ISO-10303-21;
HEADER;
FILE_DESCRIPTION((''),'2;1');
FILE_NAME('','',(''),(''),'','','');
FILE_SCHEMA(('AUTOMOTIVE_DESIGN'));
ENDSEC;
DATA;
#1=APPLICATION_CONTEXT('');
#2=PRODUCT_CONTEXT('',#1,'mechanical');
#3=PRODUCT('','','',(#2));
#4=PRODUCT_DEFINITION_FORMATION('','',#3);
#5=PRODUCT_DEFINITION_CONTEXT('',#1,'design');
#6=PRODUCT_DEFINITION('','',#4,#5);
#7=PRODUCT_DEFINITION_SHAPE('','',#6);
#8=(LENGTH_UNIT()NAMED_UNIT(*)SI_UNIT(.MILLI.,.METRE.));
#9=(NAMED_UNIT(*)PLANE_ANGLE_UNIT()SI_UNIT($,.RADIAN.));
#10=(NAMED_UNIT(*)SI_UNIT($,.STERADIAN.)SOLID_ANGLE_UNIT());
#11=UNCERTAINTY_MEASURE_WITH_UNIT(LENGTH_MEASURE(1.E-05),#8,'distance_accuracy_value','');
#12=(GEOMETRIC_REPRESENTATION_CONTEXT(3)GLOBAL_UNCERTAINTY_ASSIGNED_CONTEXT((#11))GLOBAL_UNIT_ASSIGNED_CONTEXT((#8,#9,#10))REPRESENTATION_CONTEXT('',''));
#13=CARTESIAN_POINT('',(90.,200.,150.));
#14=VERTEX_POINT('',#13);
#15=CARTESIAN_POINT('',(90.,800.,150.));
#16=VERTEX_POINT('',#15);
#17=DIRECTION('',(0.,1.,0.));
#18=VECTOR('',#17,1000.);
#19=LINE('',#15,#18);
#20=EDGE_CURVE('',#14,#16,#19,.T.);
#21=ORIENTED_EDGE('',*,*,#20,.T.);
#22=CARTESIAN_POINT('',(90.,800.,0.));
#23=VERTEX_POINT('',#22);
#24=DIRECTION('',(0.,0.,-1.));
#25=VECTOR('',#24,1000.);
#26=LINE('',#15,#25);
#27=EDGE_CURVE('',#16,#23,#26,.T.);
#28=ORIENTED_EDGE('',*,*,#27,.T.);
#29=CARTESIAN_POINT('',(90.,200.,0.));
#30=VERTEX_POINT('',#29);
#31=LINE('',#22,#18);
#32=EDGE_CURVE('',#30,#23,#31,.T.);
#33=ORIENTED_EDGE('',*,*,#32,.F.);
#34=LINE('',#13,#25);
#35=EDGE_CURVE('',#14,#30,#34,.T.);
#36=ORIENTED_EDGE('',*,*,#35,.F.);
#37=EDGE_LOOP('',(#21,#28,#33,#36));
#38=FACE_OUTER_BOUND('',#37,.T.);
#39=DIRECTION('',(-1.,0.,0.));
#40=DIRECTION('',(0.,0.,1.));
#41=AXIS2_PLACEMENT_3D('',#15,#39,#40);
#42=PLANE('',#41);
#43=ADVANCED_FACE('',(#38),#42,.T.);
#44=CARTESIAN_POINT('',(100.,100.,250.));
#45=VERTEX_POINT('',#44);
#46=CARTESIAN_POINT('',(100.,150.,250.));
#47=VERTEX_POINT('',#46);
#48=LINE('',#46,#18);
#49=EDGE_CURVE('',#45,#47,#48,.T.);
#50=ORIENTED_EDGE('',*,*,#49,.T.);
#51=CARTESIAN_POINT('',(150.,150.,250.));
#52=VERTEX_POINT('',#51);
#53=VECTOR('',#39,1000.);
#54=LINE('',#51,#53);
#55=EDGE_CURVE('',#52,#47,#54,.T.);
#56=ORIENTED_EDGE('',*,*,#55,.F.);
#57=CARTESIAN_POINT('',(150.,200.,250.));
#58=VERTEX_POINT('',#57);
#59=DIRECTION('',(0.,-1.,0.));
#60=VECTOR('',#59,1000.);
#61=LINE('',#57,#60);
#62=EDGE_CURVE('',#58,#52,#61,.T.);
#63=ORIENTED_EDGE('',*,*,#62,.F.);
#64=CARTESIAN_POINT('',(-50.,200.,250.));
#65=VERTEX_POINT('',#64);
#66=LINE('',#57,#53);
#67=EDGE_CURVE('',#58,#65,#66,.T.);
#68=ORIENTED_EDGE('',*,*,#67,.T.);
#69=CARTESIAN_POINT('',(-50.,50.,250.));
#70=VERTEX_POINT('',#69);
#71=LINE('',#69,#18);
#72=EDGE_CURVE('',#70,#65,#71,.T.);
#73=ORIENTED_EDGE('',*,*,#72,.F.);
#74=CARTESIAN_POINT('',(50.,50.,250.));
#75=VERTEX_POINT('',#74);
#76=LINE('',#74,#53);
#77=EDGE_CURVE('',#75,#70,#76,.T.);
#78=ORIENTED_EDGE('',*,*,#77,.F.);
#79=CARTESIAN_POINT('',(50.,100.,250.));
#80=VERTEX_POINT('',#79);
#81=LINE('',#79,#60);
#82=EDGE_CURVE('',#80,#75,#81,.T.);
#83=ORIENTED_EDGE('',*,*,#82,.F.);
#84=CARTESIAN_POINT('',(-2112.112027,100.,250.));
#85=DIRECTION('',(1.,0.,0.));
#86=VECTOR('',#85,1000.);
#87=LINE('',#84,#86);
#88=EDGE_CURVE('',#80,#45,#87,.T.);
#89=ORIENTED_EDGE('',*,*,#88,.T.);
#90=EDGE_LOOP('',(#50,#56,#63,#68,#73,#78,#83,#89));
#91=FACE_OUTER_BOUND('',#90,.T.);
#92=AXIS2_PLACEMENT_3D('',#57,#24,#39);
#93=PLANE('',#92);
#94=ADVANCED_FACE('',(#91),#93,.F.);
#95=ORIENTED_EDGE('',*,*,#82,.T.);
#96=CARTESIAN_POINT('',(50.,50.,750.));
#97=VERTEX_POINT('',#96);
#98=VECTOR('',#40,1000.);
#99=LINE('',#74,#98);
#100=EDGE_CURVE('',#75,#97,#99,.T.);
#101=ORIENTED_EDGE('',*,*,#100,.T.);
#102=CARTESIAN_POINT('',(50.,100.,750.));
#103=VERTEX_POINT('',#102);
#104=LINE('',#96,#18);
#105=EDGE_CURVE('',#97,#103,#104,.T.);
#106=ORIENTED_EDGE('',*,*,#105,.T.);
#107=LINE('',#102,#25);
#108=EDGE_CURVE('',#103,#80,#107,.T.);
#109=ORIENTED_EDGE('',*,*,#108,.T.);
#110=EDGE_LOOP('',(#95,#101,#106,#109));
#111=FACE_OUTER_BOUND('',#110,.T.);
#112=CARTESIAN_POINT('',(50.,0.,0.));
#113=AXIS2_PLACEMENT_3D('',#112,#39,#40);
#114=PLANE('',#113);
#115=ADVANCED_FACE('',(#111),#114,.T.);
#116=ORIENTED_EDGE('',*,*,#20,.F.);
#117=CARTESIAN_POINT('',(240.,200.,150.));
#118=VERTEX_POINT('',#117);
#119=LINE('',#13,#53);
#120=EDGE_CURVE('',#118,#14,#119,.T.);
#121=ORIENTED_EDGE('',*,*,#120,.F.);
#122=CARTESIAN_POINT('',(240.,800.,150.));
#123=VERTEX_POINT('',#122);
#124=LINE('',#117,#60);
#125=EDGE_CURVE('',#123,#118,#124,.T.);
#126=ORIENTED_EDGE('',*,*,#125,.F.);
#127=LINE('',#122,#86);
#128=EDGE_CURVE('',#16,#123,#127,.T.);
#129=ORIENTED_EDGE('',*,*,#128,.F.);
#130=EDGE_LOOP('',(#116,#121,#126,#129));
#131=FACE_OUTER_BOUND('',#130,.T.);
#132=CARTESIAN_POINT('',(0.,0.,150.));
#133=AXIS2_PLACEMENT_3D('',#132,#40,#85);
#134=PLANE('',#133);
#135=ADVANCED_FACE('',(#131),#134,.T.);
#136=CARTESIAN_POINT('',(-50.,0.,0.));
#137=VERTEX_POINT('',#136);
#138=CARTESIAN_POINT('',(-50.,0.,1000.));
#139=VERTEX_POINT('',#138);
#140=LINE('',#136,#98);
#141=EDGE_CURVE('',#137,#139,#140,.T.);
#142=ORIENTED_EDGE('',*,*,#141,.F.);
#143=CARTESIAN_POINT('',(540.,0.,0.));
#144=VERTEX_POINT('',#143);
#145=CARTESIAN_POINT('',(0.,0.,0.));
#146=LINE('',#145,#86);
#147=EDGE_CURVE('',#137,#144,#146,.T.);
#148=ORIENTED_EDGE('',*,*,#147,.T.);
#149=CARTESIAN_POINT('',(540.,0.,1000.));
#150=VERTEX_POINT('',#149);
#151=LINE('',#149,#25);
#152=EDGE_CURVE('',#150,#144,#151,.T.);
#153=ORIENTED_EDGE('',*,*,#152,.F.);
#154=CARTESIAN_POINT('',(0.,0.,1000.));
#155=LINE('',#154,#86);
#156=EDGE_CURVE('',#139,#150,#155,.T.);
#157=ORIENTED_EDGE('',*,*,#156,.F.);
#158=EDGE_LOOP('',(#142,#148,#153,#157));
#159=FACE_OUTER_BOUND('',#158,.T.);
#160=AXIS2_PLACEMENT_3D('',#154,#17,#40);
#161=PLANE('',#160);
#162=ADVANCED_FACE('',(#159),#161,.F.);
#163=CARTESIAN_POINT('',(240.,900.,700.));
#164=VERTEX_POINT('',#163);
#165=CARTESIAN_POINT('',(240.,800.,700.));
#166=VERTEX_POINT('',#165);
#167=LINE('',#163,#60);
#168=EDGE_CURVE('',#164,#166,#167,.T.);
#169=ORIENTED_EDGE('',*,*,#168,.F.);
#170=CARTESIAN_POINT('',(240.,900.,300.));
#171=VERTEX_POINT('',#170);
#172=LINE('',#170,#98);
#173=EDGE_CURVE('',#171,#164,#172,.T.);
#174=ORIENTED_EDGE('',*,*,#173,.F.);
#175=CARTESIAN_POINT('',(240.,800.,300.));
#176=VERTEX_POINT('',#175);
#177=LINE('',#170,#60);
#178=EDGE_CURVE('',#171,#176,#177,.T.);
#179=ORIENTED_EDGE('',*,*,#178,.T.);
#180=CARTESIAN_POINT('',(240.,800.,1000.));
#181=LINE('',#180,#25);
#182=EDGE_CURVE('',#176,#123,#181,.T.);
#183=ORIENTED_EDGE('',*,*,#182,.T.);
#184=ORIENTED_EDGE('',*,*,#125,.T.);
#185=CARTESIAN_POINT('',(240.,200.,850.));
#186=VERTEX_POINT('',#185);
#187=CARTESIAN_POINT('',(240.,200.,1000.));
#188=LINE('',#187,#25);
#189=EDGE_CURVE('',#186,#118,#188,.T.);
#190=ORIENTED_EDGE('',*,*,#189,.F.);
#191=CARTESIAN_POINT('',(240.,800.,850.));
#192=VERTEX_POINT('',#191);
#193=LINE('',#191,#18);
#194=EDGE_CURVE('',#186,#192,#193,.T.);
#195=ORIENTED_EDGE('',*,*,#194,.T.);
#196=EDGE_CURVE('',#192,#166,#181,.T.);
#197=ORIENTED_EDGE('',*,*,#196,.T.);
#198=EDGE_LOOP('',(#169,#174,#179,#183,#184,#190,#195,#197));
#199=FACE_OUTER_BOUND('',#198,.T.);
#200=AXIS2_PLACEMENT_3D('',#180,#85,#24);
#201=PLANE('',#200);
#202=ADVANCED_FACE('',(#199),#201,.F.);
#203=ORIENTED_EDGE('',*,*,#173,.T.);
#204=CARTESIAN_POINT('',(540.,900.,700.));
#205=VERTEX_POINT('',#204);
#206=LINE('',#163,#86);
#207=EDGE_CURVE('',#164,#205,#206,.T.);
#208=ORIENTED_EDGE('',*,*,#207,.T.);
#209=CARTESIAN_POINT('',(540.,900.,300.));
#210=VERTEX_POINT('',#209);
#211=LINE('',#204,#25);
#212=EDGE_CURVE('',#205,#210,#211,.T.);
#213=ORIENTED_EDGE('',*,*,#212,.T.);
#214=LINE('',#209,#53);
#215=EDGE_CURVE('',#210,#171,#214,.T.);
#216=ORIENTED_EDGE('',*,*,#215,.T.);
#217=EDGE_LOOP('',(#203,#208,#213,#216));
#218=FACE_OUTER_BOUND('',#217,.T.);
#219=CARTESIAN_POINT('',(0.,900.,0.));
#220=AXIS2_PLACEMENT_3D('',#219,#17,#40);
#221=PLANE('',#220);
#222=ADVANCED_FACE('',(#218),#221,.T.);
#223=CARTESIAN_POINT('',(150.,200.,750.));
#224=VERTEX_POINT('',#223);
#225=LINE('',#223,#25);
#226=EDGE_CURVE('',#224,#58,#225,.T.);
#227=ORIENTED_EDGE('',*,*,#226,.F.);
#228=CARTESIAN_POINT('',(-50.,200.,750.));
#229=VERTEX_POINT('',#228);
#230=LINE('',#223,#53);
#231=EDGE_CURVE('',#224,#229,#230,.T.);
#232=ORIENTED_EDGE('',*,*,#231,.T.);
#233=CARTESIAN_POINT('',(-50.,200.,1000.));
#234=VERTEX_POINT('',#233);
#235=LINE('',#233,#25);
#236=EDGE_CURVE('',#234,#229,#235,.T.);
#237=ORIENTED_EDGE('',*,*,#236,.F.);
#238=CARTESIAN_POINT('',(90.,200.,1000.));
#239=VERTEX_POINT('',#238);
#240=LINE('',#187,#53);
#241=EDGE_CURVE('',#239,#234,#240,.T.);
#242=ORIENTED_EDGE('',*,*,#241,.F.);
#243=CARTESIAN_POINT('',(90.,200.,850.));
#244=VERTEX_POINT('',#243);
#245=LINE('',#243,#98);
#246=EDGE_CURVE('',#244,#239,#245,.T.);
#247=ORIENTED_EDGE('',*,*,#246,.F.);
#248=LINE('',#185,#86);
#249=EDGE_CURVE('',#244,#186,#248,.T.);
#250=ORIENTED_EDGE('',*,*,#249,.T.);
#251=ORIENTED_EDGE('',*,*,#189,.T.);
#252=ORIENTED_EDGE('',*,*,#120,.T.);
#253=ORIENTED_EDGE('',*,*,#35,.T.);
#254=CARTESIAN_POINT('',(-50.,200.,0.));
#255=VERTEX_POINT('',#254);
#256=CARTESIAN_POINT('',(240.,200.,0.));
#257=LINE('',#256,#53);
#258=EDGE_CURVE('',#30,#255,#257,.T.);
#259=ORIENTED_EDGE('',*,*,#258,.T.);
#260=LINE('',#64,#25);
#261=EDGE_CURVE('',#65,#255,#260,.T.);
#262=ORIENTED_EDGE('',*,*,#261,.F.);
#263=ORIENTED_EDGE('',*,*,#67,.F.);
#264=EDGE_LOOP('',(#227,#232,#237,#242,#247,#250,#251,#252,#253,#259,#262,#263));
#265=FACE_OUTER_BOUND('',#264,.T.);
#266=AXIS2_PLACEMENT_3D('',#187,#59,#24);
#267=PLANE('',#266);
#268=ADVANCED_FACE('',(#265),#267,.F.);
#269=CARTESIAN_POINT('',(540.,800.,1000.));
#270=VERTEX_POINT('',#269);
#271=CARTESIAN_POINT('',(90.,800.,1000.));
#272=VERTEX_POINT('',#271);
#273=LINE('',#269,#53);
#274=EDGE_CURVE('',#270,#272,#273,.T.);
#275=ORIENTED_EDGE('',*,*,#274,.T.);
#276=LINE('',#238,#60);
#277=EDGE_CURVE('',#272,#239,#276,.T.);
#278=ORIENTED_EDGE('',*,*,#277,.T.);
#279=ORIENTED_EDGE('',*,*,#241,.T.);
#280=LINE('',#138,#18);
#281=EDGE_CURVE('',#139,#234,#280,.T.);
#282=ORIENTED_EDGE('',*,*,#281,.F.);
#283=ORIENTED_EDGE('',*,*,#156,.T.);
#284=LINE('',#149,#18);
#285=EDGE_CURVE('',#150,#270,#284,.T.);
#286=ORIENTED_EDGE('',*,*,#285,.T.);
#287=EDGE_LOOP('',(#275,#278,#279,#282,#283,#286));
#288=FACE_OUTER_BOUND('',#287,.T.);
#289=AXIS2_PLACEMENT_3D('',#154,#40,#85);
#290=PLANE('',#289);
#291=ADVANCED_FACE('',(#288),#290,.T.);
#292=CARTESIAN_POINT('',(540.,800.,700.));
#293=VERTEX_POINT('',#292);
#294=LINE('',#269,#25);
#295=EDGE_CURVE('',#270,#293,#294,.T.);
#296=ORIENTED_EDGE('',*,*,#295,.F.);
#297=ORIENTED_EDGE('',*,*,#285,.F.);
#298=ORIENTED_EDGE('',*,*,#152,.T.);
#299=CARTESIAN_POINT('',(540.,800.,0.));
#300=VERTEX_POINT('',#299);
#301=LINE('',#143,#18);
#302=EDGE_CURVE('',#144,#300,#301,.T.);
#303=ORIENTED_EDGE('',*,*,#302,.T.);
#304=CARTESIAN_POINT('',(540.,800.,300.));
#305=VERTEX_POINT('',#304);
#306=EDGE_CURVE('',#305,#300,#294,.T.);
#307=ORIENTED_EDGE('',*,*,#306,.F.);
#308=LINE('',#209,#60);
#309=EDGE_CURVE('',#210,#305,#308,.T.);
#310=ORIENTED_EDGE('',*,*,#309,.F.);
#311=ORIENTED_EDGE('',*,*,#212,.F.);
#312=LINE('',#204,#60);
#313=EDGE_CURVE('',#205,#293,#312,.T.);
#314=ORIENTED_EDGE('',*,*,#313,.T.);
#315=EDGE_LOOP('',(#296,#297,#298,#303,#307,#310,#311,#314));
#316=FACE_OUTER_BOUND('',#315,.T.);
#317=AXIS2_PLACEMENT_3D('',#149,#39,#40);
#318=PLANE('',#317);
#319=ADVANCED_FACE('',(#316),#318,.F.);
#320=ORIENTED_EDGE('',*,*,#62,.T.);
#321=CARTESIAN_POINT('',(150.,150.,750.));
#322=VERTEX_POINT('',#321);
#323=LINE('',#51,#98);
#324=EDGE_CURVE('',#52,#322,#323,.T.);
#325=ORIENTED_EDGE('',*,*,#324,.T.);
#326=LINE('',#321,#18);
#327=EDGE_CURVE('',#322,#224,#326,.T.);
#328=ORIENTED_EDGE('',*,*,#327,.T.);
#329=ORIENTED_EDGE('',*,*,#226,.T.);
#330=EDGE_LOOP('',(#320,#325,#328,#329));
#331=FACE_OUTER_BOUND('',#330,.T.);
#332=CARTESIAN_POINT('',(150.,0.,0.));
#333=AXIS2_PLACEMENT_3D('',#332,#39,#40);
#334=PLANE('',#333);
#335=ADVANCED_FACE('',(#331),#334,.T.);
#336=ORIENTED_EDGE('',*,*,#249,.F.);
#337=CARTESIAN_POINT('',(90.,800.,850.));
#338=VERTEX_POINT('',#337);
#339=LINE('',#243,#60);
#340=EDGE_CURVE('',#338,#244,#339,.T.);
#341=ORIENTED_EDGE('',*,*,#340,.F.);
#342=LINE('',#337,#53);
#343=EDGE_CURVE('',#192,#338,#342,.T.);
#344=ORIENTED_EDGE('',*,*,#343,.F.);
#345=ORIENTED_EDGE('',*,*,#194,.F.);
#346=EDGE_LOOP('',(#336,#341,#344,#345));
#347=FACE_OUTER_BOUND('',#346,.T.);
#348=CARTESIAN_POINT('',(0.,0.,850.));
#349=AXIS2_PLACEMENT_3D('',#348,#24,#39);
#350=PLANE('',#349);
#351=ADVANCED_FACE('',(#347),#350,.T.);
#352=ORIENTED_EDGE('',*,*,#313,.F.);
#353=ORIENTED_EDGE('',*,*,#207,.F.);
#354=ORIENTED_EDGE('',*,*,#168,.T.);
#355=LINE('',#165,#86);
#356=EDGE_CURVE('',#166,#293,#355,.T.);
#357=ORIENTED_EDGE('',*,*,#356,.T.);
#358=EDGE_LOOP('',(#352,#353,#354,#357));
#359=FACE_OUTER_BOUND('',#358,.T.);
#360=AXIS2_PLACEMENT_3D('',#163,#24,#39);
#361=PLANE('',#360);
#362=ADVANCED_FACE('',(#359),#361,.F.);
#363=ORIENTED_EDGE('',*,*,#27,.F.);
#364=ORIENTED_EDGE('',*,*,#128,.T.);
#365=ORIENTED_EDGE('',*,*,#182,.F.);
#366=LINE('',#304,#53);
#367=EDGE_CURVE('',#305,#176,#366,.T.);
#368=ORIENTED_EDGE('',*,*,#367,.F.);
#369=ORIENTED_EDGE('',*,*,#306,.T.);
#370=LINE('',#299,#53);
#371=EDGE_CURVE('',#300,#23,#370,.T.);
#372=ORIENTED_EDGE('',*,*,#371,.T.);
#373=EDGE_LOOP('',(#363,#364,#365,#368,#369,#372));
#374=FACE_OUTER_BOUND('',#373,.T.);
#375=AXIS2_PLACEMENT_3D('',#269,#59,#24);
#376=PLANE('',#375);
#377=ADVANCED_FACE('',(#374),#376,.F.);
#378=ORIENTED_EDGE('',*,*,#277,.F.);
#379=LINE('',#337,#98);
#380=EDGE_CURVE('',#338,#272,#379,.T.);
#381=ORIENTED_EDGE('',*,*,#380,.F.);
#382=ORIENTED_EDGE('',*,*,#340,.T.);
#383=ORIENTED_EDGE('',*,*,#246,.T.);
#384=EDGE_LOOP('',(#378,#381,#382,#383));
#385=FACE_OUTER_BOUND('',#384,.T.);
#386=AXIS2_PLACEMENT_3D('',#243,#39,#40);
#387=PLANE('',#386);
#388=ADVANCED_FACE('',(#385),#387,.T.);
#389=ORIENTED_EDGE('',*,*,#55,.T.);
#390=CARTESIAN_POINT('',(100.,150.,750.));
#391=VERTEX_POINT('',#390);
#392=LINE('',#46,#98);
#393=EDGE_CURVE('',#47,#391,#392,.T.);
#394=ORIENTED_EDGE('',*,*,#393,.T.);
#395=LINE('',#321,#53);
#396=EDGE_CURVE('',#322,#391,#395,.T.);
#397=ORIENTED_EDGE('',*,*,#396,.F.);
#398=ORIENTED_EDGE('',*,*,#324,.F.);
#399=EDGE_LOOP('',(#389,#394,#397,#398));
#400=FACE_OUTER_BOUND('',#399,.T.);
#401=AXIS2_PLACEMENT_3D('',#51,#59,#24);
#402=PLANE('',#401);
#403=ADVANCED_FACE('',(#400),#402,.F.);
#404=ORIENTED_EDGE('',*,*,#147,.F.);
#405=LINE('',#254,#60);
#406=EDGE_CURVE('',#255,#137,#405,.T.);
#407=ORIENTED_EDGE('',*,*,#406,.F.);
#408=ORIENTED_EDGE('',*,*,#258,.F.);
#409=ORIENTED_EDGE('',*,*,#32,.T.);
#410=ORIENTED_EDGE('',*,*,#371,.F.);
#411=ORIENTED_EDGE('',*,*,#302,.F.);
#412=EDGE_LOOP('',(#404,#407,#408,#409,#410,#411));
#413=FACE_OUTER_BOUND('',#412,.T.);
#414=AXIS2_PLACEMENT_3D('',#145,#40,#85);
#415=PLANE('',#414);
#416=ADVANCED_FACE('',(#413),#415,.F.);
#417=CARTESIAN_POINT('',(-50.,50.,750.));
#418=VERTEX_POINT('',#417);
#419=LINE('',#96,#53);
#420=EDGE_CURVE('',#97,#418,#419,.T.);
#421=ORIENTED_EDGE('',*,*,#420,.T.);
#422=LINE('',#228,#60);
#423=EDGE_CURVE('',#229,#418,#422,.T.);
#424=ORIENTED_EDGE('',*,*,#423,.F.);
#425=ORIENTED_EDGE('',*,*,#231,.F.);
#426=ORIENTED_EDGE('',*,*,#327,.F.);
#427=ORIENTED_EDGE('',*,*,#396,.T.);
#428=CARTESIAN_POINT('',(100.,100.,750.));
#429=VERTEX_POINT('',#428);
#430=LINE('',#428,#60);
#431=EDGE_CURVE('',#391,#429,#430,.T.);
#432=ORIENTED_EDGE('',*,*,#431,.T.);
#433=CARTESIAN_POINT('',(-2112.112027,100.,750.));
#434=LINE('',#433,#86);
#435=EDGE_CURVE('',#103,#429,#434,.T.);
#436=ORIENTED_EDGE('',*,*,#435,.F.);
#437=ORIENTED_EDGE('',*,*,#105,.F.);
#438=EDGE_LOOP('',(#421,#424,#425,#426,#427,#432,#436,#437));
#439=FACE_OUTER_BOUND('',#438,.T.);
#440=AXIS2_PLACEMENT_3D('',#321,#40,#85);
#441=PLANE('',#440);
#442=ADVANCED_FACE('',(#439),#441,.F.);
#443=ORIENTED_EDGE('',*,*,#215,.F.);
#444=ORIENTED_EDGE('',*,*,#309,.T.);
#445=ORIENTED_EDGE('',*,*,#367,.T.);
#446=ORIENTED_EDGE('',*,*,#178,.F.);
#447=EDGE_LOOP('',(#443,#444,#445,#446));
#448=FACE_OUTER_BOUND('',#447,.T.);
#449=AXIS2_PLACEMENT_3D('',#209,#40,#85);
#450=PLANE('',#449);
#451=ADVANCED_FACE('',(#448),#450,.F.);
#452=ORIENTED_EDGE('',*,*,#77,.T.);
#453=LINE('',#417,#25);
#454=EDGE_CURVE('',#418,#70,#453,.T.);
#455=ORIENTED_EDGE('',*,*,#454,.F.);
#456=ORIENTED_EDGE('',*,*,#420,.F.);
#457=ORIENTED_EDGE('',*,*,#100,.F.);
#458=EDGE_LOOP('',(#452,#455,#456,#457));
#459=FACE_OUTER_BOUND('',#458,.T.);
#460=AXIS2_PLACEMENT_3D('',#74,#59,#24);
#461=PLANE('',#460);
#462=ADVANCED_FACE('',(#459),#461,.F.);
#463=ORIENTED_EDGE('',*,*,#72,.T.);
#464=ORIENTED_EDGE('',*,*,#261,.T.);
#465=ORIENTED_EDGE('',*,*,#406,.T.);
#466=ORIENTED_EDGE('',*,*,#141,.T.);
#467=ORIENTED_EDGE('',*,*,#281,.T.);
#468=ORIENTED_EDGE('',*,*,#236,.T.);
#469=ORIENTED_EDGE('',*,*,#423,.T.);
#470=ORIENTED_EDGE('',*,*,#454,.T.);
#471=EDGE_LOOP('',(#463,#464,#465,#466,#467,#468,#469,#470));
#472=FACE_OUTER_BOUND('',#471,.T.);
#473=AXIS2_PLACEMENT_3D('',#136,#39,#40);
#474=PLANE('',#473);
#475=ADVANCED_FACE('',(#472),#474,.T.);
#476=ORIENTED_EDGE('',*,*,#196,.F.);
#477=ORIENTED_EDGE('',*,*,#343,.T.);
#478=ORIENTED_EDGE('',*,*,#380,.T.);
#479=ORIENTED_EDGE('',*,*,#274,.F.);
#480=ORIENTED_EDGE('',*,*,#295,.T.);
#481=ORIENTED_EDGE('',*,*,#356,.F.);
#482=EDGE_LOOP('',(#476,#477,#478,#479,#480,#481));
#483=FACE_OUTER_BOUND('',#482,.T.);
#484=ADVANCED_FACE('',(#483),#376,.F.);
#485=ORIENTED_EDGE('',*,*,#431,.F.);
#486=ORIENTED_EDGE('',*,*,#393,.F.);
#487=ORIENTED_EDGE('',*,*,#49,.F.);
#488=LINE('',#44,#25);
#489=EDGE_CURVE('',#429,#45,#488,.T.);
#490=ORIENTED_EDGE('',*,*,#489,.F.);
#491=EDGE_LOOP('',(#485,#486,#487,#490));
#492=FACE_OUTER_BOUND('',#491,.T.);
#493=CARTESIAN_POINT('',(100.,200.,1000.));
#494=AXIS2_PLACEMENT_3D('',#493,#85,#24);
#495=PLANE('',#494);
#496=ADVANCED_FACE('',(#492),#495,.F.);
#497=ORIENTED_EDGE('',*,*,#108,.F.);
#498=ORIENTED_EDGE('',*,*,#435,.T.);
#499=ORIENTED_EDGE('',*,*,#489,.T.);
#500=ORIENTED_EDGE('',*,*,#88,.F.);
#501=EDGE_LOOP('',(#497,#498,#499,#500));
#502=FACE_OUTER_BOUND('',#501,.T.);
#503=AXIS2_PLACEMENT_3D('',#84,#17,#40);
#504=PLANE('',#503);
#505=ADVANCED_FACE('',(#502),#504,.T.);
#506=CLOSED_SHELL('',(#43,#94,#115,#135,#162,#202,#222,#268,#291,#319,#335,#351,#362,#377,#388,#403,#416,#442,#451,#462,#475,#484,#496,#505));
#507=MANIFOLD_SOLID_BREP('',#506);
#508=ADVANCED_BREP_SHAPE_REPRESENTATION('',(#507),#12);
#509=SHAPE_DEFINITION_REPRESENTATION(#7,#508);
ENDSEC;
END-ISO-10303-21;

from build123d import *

# Parameters (mm, degrees)
BASE_BLOCK_DEPTH          = 1000
SIDE_BOSS_A_SKETCH_W      = 150
SIDE_BOSS_A_SKETCH_H      = 600
SIDE_BOSS_A_DEPTH         = 150
SIDE_BOSS_B_SKETCH_W      = 150
SIDE_BOSS_B_SKETCH_H      = 600
SIDE_BOSS_B_DEPTH         = 150
CORNER_BOSS_DEPTH         = 100
TOP_STEP_CUT_DEPTH        = 150
TOP_GROOVE_CUT_DEPTH      = 1450.689621954
TOP_GROOVE_CUT_DEPTH_BACK = 100
GROOVE_NOTCH_SKETCH_W     = 500
GROOVE_NOTCH_SKETCH_H     = 50
GROOVE_NOTCH_CUT_DEPTH    = 50
GROOVE_INFILL_BOSS_DEPTH  = 50


with BuildPart() as part:
    # Base Profile Sketch → Base Block (new body)
    with BuildSketch(Plane.XY):
        Polygon((0, 0), (540, 0), (540, 800), (240, 800), (240, 200), (0, 200), align=None)
    extrude(amount=BASE_BLOCK_DEPTH)

    # Side Boss A Sketch → Side Boss A (add)
    with BuildSketch(Plane(origin=(0, 0, 0), x_dir=(-1, 0, 0), z_dir=(0, 0, -1))):
        with Locations((-165, 500)):
            Rectangle(SIDE_BOSS_A_SKETCH_W, SIDE_BOSS_A_SKETCH_H)
    extrude(amount=-SIDE_BOSS_A_DEPTH)

    # Side Boss B Sketch → Side Boss B (add)
    with BuildSketch(Plane.XY.offset(1000)):
        with Locations((165, 500)):
            Rectangle(SIDE_BOSS_B_SKETCH_W, SIDE_BOSS_B_SKETCH_H)
    extrude(amount=-SIDE_BOSS_B_DEPTH)

    # Corner Boss Sketch → Corner Boss (add)
    with BuildSketch(Plane(origin=(0, 800, 0), x_dir=(1, 0, 0), z_dir=(0, 1, 0))):
        Polygon((540, -500), (540, -300), (240, -300), (240, -700), (540, -700), align=None)
    extrude(amount=CORNER_BOSS_DEPTH)

    # Top Step Cut Sketch → Top Step Cut (cut)
    with BuildSketch(Plane.ZY):
        Polygon((500, 200), (250, 200), (250, 150), (750, 150), (750, 200), align=None)
    extrude(amount=-TOP_STEP_CUT_DEPTH, mode=Mode.SUBTRACT)

    # Top Groove Sketch → Top Groove Cut (cut, two sides: drawn at the far end of the back side and taken through both)
    with BuildSketch(Plane.ZY.offset(-TOP_GROOVE_CUT_DEPTH_BACK)):
        Polygon((250, 2281.32034356), (250, 150), (250, 100), (750, 100), (750, 150), (750, 2281.32034356), (750, 6543.961030679), (250, 6543.961030679), align=None)
    extrude(amount=TOP_GROOVE_CUT_DEPTH + TOP_GROOVE_CUT_DEPTH_BACK, mode=Mode.SUBTRACT)

    # Groove Notch Sketch → Groove Notch Cut (cut)
    with BuildSketch(Plane.ZY):
        with Locations((500, 75)):
            Rectangle(GROOVE_NOTCH_SKETCH_W, GROOVE_NOTCH_SKETCH_H)
    extrude(amount=-GROOVE_NOTCH_CUT_DEPTH, mode=Mode.SUBTRACT)

    # Groove Infill Sketch → Groove Infill Boss (add)
    with BuildSketch(Plane.ZY):
        Polygon((0, 200), (0, 0), (1000, 0), (1000, 200), (750, 200), (750, 50), (250, 50), (250, 200), align=None)
    extrude(amount=GROOVE_INFILL_BOSS_DEPTH)


solid = part.part
